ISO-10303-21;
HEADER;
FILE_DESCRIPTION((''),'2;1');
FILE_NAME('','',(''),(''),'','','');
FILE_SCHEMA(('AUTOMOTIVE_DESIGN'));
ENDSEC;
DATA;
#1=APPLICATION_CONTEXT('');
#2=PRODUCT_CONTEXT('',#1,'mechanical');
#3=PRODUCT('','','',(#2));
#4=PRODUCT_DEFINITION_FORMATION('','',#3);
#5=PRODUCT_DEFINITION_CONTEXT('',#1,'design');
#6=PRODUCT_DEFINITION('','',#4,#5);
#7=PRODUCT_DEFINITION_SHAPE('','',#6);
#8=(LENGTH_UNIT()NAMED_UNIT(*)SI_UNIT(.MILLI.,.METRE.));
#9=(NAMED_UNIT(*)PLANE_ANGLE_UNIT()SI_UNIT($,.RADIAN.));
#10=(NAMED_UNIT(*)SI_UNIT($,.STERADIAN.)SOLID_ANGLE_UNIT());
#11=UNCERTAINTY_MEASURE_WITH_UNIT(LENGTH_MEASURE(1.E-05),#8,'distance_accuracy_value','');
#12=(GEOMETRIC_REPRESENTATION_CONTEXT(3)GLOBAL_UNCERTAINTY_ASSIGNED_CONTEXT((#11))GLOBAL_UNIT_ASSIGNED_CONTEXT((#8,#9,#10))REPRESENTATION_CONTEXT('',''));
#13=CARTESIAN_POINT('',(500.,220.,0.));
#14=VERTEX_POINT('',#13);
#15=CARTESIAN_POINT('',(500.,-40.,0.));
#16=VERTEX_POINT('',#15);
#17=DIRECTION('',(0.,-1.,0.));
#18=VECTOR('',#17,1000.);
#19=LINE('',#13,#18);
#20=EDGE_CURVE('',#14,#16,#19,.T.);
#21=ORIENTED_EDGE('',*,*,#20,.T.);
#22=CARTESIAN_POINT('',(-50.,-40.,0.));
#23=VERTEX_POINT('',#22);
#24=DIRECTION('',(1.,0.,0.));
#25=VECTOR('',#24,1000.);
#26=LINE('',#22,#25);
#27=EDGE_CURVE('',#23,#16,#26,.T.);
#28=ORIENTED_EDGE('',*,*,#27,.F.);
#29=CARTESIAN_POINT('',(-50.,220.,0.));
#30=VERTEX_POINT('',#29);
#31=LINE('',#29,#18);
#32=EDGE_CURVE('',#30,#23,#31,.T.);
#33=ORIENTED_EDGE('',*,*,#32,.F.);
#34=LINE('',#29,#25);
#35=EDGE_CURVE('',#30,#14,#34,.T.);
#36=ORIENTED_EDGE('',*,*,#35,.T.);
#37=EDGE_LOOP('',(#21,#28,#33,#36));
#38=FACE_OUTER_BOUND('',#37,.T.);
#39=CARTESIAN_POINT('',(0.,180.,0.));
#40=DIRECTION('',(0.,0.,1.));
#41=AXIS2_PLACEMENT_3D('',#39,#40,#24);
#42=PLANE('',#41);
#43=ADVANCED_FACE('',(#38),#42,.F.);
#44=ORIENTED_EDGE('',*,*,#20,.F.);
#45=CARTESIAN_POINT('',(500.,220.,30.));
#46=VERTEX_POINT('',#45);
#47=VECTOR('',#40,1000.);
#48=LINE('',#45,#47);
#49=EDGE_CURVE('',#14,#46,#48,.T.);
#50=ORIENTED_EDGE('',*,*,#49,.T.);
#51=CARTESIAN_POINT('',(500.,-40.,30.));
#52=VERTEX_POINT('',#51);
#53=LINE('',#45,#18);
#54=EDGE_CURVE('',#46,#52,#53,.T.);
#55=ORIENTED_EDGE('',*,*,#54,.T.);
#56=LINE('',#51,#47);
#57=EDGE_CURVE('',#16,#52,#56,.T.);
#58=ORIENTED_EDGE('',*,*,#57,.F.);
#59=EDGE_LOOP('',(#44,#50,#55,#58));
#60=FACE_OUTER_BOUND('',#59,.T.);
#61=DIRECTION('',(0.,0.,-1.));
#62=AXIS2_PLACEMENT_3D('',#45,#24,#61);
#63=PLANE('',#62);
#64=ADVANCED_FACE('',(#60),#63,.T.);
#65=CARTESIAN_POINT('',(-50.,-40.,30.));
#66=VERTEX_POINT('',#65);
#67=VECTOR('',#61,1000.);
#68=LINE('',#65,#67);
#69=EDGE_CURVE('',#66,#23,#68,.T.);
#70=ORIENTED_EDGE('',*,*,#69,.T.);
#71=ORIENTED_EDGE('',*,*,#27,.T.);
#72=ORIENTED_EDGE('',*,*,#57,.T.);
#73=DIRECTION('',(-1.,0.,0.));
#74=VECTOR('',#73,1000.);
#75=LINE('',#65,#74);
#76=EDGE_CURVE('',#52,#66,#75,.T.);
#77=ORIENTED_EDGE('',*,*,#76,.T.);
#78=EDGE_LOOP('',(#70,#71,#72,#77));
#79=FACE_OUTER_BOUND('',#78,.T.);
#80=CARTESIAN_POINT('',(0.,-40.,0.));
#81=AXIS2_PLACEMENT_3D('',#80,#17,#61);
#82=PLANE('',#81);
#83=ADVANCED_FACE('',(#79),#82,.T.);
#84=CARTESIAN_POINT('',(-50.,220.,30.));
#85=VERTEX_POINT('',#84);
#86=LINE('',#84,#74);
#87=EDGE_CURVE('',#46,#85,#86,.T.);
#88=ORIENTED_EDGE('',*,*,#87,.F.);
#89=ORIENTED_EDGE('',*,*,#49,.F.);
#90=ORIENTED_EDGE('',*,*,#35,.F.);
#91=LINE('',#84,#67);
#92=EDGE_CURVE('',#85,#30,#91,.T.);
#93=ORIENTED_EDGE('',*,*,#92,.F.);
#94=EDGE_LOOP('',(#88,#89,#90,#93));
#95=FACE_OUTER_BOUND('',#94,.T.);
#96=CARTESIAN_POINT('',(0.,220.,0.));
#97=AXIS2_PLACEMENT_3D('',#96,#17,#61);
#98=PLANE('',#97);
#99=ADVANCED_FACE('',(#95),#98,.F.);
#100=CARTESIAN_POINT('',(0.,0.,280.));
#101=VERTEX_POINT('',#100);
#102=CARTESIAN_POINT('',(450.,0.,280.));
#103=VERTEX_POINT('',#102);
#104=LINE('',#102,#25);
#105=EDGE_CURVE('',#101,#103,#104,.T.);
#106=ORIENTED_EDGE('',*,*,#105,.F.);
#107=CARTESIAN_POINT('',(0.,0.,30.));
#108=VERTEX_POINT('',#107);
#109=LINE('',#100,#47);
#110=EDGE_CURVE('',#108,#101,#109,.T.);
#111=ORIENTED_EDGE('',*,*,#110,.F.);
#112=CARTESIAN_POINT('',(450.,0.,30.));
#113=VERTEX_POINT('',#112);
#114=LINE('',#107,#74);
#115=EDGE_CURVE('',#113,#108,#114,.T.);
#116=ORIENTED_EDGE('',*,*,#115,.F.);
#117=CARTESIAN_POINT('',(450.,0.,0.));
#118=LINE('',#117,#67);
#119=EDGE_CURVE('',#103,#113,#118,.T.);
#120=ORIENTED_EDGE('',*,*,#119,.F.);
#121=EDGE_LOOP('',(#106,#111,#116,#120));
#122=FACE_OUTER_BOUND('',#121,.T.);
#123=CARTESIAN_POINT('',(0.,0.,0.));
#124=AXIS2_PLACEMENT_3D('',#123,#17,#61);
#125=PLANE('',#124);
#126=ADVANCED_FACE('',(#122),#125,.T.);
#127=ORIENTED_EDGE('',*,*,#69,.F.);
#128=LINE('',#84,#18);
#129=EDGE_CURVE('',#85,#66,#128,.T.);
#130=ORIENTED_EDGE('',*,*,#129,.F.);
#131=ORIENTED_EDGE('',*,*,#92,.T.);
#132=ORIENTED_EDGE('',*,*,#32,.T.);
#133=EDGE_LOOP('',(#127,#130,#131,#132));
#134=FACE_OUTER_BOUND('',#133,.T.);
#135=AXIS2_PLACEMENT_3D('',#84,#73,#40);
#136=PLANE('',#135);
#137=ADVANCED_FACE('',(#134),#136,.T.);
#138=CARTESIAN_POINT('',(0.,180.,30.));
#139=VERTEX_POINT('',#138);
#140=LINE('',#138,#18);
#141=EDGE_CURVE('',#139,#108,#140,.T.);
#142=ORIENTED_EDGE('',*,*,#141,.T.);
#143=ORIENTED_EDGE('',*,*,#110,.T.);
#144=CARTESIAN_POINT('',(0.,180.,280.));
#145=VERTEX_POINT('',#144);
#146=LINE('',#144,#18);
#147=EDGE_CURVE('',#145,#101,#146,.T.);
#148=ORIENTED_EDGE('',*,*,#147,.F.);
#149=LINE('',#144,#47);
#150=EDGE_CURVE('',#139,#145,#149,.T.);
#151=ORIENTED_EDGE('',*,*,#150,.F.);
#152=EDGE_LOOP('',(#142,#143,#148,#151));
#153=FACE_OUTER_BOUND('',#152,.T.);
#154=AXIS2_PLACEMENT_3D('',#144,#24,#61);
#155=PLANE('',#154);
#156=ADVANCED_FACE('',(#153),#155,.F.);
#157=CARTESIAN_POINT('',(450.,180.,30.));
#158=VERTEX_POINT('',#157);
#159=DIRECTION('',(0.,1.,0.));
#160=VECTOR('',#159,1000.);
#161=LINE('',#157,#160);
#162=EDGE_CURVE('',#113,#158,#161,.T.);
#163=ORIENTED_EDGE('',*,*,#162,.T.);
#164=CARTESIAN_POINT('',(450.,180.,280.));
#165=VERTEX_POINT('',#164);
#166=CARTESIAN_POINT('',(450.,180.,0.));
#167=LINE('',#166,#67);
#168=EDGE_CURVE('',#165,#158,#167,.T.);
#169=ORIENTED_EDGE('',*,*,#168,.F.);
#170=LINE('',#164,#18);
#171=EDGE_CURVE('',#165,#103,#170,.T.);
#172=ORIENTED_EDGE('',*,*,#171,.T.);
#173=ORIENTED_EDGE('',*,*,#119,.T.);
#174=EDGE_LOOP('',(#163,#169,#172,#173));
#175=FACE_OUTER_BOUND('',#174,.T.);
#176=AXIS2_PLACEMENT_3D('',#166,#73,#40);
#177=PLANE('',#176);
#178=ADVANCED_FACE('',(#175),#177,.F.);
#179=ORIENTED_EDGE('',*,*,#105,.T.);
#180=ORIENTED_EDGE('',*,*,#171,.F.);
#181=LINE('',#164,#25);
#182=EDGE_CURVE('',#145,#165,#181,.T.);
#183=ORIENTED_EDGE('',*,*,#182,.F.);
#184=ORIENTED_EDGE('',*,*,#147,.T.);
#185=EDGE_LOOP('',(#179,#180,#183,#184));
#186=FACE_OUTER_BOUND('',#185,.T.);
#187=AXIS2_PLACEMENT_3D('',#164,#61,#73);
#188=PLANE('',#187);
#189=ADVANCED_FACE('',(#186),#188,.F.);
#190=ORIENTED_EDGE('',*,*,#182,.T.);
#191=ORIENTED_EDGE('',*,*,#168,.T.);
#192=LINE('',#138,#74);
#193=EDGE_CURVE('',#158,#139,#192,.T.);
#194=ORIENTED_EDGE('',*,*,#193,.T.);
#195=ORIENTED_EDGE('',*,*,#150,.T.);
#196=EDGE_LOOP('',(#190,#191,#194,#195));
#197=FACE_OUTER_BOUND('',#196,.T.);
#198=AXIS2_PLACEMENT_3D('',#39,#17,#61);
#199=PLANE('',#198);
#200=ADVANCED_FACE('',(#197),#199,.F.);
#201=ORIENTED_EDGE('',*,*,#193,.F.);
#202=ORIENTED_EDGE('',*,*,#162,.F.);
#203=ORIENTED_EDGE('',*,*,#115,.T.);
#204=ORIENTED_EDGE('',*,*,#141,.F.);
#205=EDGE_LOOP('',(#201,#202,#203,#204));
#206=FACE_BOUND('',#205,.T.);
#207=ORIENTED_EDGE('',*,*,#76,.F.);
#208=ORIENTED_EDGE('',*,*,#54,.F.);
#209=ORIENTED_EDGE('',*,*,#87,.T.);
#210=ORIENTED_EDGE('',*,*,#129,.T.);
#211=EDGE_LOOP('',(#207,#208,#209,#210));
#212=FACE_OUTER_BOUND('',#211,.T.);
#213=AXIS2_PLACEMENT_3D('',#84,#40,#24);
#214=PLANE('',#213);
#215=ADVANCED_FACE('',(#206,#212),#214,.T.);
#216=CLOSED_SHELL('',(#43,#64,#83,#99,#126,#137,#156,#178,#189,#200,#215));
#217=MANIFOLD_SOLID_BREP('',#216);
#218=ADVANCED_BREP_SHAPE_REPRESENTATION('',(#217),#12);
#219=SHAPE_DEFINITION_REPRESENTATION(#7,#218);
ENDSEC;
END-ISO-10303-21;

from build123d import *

# Parameters (mm, degrees)
SKETCH1_W                = 450
SKETCH1_H                = 280
BOSS_EXTRUDE1_DEPTH      = 180
BOSS_EXTRUDE2_DEPTH      = 40
BOSS_EXTRUDE2_DEPTH_BACK = 220
SKETCH2_W                = 550
SKETCH2_H                = 30


with BuildPart() as part:
    # Sketch1 → Boss-Extrude1 (new body)
    with BuildSketch(Plane(origin=(0, 0, 0), x_dir=(1, 0, 0), z_dir=(0, 1, 0))):
        with Locations((225, -140)):
            Rectangle(SKETCH1_W, SKETCH1_H)
    extrude(amount=BOSS_EXTRUDE1_DEPTH)

    # Sketch2 → Boss-Extrude2 (add, two sides: drawn at the far end of the back side and taken through both)
    with BuildSketch(Plane.XZ.offset(-BOSS_EXTRUDE2_DEPTH_BACK)):
        with Locations((225, 15)):
            Rectangle(SKETCH2_W, SKETCH2_H)
    extrude(amount=BOSS_EXTRUDE2_DEPTH + BOSS_EXTRUDE2_DEPTH_BACK)


solid = part.part
